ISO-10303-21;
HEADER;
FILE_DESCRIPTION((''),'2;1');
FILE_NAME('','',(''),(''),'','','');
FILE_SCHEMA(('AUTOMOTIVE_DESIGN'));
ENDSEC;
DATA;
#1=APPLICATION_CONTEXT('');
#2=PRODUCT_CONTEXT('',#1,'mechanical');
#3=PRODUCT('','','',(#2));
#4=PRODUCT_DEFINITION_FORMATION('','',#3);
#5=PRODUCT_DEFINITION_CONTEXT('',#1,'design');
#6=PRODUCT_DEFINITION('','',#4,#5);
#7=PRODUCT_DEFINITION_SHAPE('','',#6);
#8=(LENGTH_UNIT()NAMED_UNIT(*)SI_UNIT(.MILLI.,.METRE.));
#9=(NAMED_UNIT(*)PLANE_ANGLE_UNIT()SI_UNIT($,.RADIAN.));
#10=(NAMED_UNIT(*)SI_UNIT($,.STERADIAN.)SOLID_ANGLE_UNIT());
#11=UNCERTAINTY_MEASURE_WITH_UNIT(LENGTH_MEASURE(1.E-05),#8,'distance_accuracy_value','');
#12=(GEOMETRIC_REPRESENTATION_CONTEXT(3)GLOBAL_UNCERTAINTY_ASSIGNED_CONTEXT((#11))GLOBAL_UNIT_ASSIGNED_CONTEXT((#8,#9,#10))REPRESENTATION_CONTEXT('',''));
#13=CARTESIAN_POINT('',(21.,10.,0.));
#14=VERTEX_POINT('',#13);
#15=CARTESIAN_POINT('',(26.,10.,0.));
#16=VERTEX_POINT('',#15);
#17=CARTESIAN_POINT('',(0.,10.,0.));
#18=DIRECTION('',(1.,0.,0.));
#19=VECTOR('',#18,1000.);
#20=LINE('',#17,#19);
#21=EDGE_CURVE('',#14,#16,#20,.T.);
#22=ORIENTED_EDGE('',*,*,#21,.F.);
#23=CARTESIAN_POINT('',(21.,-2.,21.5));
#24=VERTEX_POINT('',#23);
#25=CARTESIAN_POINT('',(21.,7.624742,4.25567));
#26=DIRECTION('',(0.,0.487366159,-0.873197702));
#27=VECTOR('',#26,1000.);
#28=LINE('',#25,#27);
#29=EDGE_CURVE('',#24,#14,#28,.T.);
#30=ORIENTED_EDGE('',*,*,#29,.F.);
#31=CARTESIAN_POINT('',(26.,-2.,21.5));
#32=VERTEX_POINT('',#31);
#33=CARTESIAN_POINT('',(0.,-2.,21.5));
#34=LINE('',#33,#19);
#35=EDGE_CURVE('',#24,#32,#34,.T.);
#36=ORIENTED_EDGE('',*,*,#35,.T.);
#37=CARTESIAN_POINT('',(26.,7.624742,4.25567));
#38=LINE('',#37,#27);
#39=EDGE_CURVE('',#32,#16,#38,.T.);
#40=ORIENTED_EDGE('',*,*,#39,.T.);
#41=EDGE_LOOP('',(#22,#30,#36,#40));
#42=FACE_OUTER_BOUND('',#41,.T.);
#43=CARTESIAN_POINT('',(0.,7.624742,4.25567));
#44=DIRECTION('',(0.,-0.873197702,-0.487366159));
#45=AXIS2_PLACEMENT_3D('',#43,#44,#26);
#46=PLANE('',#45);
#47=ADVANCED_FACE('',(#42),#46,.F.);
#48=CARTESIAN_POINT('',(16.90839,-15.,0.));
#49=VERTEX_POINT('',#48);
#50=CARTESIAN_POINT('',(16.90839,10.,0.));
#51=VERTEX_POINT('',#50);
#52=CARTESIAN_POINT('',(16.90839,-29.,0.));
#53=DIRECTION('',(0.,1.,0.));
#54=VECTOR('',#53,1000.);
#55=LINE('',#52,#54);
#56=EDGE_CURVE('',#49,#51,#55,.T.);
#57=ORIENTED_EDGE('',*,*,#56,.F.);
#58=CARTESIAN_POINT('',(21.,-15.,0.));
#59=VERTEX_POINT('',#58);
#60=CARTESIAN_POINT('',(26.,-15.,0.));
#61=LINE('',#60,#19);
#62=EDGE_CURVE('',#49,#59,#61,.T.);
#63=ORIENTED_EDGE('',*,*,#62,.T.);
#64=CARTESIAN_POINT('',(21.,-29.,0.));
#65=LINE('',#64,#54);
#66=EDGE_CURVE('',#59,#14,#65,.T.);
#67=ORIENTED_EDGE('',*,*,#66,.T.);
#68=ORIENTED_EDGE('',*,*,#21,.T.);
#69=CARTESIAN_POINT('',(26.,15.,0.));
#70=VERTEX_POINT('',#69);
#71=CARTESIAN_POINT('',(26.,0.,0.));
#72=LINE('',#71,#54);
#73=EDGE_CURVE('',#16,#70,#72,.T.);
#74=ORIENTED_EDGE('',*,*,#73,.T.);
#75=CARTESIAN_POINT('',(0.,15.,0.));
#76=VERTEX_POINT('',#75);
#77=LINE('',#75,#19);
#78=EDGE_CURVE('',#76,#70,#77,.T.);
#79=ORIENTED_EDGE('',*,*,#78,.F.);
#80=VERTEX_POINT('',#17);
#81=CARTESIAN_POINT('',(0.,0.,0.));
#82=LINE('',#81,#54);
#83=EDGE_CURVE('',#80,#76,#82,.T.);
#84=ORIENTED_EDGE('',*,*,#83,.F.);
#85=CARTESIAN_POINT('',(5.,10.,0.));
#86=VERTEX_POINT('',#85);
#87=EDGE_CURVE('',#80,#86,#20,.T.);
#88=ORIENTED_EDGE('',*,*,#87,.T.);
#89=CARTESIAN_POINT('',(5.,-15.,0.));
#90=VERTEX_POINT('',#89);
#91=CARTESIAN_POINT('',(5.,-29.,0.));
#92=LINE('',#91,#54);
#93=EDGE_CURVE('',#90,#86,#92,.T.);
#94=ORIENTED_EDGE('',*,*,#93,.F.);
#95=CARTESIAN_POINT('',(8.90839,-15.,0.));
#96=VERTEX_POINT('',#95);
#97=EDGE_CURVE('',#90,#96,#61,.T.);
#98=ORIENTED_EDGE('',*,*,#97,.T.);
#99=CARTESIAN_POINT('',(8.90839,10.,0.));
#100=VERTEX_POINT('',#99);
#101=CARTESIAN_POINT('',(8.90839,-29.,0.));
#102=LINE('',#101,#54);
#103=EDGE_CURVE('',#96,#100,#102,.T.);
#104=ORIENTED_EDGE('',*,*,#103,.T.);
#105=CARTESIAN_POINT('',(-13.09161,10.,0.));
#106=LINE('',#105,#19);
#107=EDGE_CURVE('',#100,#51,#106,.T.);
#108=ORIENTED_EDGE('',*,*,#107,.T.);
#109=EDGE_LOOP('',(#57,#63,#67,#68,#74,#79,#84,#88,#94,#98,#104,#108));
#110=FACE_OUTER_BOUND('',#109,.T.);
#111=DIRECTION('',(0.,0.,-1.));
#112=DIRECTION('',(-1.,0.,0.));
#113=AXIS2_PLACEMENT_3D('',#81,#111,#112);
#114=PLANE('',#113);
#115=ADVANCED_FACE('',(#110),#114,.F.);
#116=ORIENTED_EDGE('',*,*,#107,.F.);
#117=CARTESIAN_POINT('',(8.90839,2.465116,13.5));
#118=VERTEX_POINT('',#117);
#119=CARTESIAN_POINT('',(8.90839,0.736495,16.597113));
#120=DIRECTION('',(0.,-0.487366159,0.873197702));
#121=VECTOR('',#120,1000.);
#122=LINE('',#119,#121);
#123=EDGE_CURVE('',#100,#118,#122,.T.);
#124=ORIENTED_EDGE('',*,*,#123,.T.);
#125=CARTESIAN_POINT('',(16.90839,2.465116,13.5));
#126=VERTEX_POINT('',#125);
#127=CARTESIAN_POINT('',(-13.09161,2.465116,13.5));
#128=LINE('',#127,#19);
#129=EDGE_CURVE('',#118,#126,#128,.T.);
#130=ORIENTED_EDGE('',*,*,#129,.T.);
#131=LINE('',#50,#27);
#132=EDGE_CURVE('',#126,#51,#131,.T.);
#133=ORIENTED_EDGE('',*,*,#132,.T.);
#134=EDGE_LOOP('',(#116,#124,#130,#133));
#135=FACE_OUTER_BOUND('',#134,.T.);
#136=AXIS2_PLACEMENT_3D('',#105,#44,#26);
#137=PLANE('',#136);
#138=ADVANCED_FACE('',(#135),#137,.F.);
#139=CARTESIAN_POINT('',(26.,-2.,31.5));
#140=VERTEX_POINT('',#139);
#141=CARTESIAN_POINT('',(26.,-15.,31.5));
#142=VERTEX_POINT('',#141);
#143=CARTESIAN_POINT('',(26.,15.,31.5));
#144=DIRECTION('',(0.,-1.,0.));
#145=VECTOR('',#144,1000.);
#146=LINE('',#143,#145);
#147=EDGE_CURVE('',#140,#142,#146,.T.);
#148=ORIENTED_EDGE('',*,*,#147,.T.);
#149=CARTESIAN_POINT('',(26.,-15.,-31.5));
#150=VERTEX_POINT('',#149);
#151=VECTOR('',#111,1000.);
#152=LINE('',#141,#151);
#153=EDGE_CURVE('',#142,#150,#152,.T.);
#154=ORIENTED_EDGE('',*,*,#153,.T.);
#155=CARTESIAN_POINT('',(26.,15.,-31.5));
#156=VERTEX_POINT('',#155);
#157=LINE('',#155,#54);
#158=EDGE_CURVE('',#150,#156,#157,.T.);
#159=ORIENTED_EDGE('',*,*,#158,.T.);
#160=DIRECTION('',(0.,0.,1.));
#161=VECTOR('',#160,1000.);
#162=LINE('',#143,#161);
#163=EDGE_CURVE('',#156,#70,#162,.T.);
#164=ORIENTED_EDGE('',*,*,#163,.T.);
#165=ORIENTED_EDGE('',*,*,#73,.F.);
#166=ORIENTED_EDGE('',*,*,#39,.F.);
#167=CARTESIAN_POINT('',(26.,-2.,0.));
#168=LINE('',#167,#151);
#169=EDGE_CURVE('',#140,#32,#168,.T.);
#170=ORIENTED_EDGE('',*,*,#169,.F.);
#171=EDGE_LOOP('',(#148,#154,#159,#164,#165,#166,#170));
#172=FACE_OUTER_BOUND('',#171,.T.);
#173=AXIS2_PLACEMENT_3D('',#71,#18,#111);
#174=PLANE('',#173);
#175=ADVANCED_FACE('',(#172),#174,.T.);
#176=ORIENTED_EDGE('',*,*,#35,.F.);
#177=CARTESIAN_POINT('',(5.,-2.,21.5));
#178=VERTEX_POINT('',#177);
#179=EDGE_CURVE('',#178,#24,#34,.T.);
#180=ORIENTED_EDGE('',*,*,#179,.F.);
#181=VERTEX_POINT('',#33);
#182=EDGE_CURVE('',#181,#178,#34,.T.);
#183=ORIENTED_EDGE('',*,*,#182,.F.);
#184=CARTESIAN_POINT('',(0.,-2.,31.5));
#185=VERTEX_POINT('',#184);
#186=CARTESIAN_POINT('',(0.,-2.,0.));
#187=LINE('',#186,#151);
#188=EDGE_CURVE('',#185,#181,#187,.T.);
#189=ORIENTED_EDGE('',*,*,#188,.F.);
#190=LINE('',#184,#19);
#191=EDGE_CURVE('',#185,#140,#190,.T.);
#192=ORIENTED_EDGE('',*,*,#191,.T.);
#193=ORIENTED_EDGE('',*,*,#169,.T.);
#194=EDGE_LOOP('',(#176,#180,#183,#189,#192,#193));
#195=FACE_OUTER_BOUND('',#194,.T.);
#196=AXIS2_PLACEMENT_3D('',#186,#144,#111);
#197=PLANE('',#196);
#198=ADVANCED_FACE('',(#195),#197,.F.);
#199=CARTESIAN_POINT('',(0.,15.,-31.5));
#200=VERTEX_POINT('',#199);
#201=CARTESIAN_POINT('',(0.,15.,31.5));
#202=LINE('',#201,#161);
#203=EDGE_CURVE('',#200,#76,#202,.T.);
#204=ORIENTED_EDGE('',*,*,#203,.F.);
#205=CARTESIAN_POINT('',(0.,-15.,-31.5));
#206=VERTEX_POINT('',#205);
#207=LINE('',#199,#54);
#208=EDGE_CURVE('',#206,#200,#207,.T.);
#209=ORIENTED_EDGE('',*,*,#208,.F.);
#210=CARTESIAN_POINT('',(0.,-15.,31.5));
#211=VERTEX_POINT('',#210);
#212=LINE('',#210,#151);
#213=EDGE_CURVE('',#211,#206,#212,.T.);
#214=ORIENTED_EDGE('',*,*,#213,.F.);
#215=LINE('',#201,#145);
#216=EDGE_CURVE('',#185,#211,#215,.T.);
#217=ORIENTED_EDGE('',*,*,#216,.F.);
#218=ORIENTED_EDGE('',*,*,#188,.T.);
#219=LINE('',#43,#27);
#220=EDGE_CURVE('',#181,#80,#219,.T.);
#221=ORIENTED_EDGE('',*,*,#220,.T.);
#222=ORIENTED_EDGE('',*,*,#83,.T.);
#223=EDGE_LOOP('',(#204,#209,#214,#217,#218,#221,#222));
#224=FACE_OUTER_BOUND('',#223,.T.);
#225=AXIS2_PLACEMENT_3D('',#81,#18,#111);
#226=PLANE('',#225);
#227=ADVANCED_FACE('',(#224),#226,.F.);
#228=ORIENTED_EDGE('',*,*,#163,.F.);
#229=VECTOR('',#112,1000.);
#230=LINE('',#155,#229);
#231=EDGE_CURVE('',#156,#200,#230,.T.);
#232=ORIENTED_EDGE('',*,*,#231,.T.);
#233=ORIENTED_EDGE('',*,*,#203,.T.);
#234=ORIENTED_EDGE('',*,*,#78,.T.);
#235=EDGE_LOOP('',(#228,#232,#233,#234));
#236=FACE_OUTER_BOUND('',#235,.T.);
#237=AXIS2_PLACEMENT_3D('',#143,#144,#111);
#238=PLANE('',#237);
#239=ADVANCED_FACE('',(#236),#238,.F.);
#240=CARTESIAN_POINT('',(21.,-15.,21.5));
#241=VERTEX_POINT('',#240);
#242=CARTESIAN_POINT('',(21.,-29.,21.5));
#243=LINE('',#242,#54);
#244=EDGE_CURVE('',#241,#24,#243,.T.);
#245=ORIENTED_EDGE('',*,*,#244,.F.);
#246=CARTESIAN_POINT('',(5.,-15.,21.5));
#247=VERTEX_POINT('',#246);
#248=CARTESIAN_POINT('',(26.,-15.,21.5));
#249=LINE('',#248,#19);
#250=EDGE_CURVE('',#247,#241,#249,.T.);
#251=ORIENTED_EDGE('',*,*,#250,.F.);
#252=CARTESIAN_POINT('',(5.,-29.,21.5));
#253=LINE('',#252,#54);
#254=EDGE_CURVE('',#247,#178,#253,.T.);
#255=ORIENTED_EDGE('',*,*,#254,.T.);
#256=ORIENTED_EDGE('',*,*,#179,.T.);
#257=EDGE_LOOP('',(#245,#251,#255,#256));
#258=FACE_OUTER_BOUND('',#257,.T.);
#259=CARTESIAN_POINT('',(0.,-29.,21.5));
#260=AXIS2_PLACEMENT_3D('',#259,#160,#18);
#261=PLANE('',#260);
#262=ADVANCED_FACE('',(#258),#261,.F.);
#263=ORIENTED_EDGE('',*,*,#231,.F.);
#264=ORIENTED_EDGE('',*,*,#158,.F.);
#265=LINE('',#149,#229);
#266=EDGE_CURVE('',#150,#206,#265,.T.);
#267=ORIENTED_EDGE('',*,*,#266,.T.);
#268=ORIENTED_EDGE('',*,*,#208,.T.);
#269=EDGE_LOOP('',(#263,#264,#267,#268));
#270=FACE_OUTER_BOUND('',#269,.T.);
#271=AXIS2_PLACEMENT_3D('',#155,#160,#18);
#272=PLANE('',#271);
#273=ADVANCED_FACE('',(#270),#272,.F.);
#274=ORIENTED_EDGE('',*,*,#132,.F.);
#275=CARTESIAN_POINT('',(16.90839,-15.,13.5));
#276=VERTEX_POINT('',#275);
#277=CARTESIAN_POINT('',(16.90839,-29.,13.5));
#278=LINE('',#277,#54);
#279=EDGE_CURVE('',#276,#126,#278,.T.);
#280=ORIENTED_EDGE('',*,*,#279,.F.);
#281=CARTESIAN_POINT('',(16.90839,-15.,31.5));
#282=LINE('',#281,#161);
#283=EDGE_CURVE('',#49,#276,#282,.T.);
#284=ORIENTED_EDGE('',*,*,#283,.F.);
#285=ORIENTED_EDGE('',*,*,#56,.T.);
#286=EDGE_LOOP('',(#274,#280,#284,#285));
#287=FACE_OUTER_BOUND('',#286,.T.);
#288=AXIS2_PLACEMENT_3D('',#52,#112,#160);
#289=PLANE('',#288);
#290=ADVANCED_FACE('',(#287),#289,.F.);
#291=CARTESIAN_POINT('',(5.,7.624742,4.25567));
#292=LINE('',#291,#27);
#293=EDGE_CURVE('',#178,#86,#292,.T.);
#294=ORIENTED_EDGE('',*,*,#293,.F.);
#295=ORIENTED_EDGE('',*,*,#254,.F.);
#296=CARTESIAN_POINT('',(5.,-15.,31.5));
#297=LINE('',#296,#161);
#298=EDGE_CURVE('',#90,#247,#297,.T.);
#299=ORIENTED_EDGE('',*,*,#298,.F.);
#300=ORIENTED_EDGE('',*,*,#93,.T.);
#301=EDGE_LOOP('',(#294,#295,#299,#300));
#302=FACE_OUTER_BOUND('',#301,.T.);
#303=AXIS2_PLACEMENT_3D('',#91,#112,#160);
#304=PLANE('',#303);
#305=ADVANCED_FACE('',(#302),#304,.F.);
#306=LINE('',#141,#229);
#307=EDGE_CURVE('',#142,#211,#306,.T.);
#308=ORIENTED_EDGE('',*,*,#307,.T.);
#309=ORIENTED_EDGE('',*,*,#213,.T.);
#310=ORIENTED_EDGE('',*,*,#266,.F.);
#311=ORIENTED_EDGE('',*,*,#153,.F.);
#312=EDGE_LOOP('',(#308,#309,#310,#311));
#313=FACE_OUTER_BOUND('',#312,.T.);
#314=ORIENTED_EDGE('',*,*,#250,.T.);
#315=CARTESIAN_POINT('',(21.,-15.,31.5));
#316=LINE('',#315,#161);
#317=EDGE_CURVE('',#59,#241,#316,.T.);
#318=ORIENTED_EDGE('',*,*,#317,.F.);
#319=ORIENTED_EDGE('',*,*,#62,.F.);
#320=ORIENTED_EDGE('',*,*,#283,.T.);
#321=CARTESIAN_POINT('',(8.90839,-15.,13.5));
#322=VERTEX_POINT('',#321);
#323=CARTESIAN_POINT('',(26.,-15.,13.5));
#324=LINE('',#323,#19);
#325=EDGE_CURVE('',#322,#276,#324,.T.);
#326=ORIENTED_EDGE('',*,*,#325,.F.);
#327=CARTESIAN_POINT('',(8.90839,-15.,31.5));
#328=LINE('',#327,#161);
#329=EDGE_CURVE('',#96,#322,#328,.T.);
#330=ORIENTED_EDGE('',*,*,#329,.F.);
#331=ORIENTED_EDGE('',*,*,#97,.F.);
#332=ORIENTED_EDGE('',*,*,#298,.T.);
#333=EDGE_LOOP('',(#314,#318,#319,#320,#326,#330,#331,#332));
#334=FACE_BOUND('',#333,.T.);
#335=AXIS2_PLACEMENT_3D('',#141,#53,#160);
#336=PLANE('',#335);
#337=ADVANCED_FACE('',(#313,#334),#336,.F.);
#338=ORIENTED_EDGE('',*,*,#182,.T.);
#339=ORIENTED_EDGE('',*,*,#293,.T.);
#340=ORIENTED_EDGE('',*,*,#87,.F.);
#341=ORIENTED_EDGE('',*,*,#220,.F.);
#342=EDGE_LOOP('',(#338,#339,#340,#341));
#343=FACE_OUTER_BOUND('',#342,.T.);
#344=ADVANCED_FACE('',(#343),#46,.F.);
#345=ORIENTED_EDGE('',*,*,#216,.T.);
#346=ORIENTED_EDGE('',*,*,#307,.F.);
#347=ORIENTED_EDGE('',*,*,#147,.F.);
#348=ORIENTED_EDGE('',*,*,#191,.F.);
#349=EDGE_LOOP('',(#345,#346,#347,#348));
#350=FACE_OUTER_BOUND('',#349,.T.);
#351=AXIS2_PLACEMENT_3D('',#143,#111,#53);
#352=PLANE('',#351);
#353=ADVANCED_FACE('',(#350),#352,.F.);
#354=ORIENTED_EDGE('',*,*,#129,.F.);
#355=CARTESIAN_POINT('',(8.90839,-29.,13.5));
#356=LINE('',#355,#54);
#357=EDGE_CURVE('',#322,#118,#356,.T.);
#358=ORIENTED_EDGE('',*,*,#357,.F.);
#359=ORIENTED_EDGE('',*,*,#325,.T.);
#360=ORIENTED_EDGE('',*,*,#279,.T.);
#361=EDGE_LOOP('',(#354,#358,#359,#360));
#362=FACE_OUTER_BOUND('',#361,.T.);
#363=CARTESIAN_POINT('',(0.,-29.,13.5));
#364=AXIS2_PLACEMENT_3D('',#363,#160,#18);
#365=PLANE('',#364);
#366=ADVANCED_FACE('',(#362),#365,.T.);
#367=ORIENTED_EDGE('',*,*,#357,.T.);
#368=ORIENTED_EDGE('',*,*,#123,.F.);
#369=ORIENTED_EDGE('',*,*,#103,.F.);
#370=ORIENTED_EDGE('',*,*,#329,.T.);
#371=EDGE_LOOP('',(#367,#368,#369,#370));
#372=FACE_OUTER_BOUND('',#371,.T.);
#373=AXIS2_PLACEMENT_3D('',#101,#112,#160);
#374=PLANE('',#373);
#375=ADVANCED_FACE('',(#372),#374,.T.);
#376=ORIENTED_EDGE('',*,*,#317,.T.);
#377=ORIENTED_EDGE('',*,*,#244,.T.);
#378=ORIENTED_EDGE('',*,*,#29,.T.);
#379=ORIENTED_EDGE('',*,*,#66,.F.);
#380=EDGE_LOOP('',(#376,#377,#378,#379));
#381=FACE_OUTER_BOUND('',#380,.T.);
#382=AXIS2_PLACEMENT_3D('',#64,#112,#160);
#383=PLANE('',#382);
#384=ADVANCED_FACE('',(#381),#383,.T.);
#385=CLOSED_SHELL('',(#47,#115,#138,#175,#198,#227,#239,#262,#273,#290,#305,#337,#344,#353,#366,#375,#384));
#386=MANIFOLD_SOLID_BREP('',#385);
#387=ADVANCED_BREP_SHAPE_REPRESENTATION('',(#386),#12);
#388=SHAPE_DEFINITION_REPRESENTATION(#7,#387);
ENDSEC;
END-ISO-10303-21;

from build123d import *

# Parameters (mm, degrees)
BASE_BLOCK_PROFILE_W       = 63
BASE_BLOCK_PROFILE_H       = 30
BASE_BLOCK_DEPTH           = 26
STEPPED_SLOPE_CUT_DEPTH    = 26
INCLINED_CHANNEL_CUT_DEPTH = 44
CENTRE_RIB_PROFILE_W       = 8
CENTRE_RIB_PROFILE_H       = 25.036205804
CENTRE_RIB_DEPTH           = 30
TOP_NOTCH_CUT_DEPTH        = 30


with BuildPart() as part:
    # Base Block Profile → Base Block (new body)
    with BuildSketch(Plane(origin=(0, 0, 0), x_dir=(0, 0, -1), z_dir=(1, 0, 0))):
        Rectangle(BASE_BLOCK_PROFILE_W, BASE_BLOCK_PROFILE_H)
    extrude(amount=BASE_BLOCK_DEPTH)

    # Stepped Slope Profile → Stepped Slope Cut (cut)
    with BuildSketch(Plane(origin=(26, 0, 0), x_dir=(0, 0, -1), z_dir=(1, 0, 0))):
        Polygon((-31.5, 15), (-31.5, -2), (-21.5, -2), (0, 10), (0, 15), align=None)
    extrude(amount=-STEPPED_SLOPE_CUT_DEPTH, mode=Mode.SUBTRACT)

    # Inclined Channel Profile → Inclined Channel Cut (cut)
    with BuildSketch(Plane(origin=(0, 15, 0), x_dir=(1, 0, 0), z_dir=(0, 1, 0))):
        Polygon((8.908390329, 0), (5, 0), (5, -21.5), (21, -21.5), (21, 0), (16.908390329, 0), (16.908390329, -13.5), (8.908390329, -13.5), align=None)
    extrude(amount=-INCLINED_CHANNEL_CUT_DEPTH, mode=Mode.SUBTRACT)

    # Centre Rib Profile → Centre Rib (add)
    with BuildSketch(Plane.XZ.offset(15)):
        with Locations((12.908390329, 0.981897098)):
            Rectangle(CENTRE_RIB_PROFILE_W, CENTRE_RIB_PROFILE_H)
    extrude(amount=-CENTRE_RIB_DEPTH)

    # Notch Profile → Top Notch Cut (cut)
    with BuildSketch(Plane(origin=(16.908390329, 0, 0), x_dir=(0, 0, -1), z_dir=(1, 0, 0))):
        Polygon((0, 10), (-13.5, 2.465116279), (-13.5, 15), (0, 15), align=None)
    extrude(amount=-TOP_NOTCH_CUT_DEPTH, mode=Mode.SUBTRACT)


solid = part.part
